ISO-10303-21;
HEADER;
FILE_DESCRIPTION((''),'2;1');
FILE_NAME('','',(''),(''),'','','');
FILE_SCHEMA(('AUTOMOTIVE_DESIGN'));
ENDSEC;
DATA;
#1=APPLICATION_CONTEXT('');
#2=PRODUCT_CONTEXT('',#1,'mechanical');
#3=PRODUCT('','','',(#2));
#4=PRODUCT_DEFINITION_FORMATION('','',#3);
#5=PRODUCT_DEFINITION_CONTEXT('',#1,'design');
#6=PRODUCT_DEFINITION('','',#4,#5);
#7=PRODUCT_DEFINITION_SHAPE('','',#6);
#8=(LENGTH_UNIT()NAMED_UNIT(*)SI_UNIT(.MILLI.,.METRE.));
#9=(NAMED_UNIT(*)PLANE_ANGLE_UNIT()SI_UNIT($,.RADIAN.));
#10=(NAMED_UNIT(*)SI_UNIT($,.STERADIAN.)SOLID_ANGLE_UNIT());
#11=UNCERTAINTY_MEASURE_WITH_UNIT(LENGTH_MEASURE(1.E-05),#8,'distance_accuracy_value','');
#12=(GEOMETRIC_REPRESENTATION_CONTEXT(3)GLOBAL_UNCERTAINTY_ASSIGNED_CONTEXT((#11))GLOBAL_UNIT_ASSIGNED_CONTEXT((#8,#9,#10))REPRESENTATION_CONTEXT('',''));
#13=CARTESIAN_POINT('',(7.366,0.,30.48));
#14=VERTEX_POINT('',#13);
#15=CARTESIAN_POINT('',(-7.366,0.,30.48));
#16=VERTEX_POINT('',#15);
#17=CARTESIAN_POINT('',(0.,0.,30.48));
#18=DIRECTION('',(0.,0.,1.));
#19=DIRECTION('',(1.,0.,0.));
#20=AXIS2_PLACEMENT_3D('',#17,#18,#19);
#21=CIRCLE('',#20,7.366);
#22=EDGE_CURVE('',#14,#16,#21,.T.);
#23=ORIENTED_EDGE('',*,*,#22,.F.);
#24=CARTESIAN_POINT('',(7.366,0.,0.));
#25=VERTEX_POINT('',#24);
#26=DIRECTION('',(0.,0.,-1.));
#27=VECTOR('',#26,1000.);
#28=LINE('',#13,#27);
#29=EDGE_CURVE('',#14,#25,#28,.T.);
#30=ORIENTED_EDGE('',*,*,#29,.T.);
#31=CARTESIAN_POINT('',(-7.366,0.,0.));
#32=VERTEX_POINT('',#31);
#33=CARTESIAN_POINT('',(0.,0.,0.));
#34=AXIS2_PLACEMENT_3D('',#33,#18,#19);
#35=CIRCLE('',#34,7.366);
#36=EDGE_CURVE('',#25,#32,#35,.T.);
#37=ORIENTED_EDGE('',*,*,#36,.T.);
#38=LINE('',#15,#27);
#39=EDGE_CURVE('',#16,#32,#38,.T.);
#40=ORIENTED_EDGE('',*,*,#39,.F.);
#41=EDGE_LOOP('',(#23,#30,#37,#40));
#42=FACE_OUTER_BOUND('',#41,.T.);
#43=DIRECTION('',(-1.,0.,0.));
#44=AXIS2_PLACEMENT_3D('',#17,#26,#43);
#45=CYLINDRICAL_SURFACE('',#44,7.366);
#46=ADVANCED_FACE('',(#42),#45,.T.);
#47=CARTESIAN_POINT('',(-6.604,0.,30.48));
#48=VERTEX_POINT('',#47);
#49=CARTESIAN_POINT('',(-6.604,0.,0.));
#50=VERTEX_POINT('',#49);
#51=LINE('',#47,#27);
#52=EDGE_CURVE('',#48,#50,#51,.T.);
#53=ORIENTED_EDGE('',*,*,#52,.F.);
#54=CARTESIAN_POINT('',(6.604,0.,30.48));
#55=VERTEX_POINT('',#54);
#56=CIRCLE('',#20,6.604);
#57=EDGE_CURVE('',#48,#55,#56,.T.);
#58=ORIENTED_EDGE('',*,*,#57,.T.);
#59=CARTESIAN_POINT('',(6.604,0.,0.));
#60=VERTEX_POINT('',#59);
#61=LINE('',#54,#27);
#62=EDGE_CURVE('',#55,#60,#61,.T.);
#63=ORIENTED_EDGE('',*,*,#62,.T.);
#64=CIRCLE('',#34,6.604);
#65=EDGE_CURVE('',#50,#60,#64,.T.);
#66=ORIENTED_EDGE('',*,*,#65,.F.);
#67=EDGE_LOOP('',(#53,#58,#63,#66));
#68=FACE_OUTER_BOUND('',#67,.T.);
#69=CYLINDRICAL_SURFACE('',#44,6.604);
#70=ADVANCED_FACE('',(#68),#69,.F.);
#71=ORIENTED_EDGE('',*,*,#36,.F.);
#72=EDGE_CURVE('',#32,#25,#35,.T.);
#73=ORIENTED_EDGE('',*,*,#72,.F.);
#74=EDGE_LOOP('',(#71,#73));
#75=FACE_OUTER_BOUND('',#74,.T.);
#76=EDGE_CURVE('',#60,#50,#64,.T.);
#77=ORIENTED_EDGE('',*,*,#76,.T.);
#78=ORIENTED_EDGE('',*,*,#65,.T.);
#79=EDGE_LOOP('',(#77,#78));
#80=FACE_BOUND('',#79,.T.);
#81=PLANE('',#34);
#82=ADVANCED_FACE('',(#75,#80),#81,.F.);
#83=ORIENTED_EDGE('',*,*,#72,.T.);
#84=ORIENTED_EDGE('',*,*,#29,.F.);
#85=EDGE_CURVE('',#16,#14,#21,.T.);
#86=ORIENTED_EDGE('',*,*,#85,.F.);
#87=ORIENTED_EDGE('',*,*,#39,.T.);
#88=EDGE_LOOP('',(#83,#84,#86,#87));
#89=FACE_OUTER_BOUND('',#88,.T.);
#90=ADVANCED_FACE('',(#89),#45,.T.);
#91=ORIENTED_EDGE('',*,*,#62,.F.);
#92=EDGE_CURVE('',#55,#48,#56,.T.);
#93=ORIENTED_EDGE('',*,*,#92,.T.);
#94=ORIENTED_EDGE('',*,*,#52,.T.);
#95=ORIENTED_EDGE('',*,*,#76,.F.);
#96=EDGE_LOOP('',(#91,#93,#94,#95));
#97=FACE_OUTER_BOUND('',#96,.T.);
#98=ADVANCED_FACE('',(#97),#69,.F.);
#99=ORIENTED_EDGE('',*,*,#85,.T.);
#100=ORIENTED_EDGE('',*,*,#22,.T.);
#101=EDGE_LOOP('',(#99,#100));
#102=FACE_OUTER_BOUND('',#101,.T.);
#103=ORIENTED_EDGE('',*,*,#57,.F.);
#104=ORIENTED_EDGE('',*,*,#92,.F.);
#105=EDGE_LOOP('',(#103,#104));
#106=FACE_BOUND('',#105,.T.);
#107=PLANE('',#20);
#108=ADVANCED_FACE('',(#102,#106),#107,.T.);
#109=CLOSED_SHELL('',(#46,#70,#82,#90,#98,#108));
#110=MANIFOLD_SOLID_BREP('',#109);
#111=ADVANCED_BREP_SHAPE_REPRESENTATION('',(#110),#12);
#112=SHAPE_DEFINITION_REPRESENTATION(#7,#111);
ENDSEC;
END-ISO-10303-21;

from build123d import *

# Parameters (mm, degrees)
SKETCH1_R           = 3.683
SKETCH1_R_2         = 3.302
BOSS_EXTRUDE1_DEPTH = 15.24
SCALE1_SCALE        = 2


with BuildPart() as part:
    # Sketch1 → Boss-Extrude1 (new body)
    with BuildSketch(Plane.XY):
        with Locations(Location((0, 0, 0), (0, 0, 180))):
            Circle(SKETCH1_R)
        with Locations(Location((0, 0, 0), (0, 0, 180))):
            Circle(SKETCH1_R_2, mode=Mode.SUBTRACT)
    extrude(amount=BOSS_EXTRUDE1_DEPTH)


with BuildPart() as part_1:
    # Scale1: scaled about (0, 0, 0)
    add(part.part.scale(SCALE1_SCALE))


solid = part_1.part
